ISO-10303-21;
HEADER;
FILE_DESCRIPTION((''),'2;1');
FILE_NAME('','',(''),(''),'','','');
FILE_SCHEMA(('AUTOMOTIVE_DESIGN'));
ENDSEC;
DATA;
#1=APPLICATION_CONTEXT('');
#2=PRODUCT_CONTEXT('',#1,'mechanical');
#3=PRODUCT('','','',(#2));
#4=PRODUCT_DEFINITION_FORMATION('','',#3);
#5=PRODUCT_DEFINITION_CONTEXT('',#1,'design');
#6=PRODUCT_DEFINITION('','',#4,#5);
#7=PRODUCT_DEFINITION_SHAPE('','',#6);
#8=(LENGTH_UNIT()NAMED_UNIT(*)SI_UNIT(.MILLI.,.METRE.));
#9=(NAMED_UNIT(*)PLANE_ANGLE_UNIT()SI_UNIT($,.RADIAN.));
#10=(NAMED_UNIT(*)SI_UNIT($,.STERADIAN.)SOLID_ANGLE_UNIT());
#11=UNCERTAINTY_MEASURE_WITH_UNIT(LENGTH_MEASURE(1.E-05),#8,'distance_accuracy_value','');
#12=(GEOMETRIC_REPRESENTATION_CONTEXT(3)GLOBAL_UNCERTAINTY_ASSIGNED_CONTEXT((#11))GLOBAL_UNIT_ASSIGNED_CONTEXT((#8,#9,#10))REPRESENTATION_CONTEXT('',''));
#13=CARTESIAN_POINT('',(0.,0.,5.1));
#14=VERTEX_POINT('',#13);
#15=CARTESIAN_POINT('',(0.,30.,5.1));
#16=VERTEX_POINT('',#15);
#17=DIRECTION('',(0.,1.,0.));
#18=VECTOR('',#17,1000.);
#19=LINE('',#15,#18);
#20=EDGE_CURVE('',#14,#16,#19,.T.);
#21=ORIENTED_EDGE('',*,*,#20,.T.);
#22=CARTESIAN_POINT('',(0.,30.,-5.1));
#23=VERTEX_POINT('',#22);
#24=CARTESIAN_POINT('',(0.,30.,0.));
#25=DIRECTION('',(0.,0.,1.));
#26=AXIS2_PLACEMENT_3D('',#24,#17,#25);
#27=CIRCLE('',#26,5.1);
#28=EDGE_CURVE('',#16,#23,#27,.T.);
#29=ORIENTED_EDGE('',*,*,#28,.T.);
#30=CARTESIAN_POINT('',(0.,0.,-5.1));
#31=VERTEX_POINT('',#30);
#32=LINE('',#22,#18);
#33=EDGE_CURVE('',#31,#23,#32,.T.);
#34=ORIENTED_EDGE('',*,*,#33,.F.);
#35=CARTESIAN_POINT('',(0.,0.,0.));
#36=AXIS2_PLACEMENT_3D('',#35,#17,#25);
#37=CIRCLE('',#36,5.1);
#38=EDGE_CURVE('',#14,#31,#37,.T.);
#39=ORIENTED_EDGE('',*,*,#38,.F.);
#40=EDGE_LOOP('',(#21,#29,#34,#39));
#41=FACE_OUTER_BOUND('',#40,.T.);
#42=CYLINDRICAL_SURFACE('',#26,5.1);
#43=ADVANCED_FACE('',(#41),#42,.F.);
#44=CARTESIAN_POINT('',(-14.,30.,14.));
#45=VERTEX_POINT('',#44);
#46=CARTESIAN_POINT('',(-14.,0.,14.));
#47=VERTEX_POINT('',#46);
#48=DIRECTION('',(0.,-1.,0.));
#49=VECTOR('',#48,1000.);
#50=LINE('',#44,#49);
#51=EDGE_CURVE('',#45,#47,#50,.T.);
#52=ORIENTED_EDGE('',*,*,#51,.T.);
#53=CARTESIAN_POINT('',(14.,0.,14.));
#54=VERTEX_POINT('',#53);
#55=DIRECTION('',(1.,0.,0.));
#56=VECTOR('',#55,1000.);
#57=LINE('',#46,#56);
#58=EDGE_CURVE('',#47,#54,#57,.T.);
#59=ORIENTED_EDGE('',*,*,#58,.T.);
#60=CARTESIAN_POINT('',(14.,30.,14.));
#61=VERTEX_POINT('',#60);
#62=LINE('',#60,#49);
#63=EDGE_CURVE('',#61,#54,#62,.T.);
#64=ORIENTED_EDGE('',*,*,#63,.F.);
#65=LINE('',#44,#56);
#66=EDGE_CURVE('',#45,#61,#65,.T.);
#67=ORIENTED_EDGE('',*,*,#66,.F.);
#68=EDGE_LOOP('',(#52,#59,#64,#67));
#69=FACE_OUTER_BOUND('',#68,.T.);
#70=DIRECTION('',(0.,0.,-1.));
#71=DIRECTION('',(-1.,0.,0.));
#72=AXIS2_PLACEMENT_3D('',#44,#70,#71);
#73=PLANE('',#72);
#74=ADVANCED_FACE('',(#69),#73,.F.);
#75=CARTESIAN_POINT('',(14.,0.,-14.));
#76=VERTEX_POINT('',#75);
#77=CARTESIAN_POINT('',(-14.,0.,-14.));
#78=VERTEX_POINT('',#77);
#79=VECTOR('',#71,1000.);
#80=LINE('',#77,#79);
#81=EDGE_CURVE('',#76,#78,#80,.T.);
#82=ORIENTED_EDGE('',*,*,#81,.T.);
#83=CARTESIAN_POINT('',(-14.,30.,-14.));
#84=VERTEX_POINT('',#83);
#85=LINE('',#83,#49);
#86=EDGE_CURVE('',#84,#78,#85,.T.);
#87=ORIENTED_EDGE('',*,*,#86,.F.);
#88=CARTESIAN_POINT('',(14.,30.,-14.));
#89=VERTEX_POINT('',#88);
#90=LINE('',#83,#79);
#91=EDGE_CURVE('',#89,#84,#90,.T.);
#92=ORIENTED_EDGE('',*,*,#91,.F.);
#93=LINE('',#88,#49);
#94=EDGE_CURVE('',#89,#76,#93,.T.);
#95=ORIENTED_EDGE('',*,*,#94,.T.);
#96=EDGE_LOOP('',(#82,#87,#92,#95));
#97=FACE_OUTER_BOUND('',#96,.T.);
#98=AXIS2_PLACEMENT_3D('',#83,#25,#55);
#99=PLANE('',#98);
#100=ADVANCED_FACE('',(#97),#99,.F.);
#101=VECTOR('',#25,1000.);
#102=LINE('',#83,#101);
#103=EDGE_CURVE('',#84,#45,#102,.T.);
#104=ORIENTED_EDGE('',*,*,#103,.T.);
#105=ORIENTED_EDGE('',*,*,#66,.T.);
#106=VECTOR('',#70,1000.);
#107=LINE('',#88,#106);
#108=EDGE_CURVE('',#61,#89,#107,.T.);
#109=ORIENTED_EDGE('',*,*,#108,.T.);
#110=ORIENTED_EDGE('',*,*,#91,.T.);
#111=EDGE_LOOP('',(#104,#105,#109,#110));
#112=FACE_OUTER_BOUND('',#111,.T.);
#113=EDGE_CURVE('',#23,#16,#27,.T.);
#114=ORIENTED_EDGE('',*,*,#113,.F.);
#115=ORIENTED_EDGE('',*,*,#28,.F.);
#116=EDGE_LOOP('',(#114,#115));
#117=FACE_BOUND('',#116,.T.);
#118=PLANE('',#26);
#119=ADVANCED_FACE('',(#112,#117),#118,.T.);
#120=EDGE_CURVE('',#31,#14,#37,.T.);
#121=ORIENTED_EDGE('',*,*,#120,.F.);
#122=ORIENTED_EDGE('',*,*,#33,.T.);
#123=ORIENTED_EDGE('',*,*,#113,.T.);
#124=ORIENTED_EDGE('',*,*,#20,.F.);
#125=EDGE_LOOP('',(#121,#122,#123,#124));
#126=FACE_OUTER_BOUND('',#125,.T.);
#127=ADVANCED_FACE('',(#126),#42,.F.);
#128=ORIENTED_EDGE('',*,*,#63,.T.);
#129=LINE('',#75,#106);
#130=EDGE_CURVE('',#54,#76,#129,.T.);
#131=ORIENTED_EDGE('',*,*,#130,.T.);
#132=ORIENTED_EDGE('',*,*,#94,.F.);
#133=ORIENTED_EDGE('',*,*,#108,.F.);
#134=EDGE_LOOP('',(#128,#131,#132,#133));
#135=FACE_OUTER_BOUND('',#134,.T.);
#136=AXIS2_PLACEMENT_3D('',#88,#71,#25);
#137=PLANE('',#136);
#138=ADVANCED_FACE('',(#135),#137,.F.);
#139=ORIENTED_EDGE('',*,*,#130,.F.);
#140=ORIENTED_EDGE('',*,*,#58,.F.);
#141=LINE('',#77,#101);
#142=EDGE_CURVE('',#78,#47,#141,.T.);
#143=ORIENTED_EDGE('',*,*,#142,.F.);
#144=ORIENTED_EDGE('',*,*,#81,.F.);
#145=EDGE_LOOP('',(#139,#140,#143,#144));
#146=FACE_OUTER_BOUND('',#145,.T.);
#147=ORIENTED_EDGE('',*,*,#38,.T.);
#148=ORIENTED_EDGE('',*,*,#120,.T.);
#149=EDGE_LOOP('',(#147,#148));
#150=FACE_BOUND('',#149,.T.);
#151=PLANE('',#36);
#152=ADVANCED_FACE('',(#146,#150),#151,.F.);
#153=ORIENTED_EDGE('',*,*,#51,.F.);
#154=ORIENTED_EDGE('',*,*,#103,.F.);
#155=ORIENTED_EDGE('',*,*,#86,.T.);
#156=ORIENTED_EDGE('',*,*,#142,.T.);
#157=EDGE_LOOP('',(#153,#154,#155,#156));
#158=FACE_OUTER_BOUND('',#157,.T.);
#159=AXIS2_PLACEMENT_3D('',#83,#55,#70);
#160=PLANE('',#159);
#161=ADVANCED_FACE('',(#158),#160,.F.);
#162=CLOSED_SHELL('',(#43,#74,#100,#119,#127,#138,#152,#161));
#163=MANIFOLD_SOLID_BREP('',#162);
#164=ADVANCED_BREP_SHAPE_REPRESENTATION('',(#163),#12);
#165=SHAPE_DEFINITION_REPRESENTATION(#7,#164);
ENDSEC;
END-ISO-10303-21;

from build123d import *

# Parameters (mm, degrees)
SKETCH1_W           = 28
SKETCH1_H           = 28
SKETCH1_R           = 5
BOSS_EXTRUDE1_DEPTH = 30
M12_TAPPED_HOLE1_D  = 10.2


with BuildPart() as part:
    # Sketch1 → Boss-Extrude1 (new body)
    with BuildSketch(Plane(origin=(0, 0, 0), x_dir=(1, 0, 0), z_dir=(0, 1, 0))):
        Rectangle(SKETCH1_W, SKETCH1_H)
        with Locations(Location((0, 0, 0), (0, 0, 270))):
            Circle(SKETCH1_R, mode=Mode.SUBTRACT)
    extrude(amount=BOSS_EXTRUDE1_DEPTH)

    # M12 Tapped Hole1 (through all)
    with Locations(Plane(origin=(0, 30, 0), x_dir=(1, 0, 0), z_dir=(0, 1, 0))):
        with Locations((0, 0)):
            Hole(M12_TAPPED_HOLE1_D / 2)


solid = part.part
